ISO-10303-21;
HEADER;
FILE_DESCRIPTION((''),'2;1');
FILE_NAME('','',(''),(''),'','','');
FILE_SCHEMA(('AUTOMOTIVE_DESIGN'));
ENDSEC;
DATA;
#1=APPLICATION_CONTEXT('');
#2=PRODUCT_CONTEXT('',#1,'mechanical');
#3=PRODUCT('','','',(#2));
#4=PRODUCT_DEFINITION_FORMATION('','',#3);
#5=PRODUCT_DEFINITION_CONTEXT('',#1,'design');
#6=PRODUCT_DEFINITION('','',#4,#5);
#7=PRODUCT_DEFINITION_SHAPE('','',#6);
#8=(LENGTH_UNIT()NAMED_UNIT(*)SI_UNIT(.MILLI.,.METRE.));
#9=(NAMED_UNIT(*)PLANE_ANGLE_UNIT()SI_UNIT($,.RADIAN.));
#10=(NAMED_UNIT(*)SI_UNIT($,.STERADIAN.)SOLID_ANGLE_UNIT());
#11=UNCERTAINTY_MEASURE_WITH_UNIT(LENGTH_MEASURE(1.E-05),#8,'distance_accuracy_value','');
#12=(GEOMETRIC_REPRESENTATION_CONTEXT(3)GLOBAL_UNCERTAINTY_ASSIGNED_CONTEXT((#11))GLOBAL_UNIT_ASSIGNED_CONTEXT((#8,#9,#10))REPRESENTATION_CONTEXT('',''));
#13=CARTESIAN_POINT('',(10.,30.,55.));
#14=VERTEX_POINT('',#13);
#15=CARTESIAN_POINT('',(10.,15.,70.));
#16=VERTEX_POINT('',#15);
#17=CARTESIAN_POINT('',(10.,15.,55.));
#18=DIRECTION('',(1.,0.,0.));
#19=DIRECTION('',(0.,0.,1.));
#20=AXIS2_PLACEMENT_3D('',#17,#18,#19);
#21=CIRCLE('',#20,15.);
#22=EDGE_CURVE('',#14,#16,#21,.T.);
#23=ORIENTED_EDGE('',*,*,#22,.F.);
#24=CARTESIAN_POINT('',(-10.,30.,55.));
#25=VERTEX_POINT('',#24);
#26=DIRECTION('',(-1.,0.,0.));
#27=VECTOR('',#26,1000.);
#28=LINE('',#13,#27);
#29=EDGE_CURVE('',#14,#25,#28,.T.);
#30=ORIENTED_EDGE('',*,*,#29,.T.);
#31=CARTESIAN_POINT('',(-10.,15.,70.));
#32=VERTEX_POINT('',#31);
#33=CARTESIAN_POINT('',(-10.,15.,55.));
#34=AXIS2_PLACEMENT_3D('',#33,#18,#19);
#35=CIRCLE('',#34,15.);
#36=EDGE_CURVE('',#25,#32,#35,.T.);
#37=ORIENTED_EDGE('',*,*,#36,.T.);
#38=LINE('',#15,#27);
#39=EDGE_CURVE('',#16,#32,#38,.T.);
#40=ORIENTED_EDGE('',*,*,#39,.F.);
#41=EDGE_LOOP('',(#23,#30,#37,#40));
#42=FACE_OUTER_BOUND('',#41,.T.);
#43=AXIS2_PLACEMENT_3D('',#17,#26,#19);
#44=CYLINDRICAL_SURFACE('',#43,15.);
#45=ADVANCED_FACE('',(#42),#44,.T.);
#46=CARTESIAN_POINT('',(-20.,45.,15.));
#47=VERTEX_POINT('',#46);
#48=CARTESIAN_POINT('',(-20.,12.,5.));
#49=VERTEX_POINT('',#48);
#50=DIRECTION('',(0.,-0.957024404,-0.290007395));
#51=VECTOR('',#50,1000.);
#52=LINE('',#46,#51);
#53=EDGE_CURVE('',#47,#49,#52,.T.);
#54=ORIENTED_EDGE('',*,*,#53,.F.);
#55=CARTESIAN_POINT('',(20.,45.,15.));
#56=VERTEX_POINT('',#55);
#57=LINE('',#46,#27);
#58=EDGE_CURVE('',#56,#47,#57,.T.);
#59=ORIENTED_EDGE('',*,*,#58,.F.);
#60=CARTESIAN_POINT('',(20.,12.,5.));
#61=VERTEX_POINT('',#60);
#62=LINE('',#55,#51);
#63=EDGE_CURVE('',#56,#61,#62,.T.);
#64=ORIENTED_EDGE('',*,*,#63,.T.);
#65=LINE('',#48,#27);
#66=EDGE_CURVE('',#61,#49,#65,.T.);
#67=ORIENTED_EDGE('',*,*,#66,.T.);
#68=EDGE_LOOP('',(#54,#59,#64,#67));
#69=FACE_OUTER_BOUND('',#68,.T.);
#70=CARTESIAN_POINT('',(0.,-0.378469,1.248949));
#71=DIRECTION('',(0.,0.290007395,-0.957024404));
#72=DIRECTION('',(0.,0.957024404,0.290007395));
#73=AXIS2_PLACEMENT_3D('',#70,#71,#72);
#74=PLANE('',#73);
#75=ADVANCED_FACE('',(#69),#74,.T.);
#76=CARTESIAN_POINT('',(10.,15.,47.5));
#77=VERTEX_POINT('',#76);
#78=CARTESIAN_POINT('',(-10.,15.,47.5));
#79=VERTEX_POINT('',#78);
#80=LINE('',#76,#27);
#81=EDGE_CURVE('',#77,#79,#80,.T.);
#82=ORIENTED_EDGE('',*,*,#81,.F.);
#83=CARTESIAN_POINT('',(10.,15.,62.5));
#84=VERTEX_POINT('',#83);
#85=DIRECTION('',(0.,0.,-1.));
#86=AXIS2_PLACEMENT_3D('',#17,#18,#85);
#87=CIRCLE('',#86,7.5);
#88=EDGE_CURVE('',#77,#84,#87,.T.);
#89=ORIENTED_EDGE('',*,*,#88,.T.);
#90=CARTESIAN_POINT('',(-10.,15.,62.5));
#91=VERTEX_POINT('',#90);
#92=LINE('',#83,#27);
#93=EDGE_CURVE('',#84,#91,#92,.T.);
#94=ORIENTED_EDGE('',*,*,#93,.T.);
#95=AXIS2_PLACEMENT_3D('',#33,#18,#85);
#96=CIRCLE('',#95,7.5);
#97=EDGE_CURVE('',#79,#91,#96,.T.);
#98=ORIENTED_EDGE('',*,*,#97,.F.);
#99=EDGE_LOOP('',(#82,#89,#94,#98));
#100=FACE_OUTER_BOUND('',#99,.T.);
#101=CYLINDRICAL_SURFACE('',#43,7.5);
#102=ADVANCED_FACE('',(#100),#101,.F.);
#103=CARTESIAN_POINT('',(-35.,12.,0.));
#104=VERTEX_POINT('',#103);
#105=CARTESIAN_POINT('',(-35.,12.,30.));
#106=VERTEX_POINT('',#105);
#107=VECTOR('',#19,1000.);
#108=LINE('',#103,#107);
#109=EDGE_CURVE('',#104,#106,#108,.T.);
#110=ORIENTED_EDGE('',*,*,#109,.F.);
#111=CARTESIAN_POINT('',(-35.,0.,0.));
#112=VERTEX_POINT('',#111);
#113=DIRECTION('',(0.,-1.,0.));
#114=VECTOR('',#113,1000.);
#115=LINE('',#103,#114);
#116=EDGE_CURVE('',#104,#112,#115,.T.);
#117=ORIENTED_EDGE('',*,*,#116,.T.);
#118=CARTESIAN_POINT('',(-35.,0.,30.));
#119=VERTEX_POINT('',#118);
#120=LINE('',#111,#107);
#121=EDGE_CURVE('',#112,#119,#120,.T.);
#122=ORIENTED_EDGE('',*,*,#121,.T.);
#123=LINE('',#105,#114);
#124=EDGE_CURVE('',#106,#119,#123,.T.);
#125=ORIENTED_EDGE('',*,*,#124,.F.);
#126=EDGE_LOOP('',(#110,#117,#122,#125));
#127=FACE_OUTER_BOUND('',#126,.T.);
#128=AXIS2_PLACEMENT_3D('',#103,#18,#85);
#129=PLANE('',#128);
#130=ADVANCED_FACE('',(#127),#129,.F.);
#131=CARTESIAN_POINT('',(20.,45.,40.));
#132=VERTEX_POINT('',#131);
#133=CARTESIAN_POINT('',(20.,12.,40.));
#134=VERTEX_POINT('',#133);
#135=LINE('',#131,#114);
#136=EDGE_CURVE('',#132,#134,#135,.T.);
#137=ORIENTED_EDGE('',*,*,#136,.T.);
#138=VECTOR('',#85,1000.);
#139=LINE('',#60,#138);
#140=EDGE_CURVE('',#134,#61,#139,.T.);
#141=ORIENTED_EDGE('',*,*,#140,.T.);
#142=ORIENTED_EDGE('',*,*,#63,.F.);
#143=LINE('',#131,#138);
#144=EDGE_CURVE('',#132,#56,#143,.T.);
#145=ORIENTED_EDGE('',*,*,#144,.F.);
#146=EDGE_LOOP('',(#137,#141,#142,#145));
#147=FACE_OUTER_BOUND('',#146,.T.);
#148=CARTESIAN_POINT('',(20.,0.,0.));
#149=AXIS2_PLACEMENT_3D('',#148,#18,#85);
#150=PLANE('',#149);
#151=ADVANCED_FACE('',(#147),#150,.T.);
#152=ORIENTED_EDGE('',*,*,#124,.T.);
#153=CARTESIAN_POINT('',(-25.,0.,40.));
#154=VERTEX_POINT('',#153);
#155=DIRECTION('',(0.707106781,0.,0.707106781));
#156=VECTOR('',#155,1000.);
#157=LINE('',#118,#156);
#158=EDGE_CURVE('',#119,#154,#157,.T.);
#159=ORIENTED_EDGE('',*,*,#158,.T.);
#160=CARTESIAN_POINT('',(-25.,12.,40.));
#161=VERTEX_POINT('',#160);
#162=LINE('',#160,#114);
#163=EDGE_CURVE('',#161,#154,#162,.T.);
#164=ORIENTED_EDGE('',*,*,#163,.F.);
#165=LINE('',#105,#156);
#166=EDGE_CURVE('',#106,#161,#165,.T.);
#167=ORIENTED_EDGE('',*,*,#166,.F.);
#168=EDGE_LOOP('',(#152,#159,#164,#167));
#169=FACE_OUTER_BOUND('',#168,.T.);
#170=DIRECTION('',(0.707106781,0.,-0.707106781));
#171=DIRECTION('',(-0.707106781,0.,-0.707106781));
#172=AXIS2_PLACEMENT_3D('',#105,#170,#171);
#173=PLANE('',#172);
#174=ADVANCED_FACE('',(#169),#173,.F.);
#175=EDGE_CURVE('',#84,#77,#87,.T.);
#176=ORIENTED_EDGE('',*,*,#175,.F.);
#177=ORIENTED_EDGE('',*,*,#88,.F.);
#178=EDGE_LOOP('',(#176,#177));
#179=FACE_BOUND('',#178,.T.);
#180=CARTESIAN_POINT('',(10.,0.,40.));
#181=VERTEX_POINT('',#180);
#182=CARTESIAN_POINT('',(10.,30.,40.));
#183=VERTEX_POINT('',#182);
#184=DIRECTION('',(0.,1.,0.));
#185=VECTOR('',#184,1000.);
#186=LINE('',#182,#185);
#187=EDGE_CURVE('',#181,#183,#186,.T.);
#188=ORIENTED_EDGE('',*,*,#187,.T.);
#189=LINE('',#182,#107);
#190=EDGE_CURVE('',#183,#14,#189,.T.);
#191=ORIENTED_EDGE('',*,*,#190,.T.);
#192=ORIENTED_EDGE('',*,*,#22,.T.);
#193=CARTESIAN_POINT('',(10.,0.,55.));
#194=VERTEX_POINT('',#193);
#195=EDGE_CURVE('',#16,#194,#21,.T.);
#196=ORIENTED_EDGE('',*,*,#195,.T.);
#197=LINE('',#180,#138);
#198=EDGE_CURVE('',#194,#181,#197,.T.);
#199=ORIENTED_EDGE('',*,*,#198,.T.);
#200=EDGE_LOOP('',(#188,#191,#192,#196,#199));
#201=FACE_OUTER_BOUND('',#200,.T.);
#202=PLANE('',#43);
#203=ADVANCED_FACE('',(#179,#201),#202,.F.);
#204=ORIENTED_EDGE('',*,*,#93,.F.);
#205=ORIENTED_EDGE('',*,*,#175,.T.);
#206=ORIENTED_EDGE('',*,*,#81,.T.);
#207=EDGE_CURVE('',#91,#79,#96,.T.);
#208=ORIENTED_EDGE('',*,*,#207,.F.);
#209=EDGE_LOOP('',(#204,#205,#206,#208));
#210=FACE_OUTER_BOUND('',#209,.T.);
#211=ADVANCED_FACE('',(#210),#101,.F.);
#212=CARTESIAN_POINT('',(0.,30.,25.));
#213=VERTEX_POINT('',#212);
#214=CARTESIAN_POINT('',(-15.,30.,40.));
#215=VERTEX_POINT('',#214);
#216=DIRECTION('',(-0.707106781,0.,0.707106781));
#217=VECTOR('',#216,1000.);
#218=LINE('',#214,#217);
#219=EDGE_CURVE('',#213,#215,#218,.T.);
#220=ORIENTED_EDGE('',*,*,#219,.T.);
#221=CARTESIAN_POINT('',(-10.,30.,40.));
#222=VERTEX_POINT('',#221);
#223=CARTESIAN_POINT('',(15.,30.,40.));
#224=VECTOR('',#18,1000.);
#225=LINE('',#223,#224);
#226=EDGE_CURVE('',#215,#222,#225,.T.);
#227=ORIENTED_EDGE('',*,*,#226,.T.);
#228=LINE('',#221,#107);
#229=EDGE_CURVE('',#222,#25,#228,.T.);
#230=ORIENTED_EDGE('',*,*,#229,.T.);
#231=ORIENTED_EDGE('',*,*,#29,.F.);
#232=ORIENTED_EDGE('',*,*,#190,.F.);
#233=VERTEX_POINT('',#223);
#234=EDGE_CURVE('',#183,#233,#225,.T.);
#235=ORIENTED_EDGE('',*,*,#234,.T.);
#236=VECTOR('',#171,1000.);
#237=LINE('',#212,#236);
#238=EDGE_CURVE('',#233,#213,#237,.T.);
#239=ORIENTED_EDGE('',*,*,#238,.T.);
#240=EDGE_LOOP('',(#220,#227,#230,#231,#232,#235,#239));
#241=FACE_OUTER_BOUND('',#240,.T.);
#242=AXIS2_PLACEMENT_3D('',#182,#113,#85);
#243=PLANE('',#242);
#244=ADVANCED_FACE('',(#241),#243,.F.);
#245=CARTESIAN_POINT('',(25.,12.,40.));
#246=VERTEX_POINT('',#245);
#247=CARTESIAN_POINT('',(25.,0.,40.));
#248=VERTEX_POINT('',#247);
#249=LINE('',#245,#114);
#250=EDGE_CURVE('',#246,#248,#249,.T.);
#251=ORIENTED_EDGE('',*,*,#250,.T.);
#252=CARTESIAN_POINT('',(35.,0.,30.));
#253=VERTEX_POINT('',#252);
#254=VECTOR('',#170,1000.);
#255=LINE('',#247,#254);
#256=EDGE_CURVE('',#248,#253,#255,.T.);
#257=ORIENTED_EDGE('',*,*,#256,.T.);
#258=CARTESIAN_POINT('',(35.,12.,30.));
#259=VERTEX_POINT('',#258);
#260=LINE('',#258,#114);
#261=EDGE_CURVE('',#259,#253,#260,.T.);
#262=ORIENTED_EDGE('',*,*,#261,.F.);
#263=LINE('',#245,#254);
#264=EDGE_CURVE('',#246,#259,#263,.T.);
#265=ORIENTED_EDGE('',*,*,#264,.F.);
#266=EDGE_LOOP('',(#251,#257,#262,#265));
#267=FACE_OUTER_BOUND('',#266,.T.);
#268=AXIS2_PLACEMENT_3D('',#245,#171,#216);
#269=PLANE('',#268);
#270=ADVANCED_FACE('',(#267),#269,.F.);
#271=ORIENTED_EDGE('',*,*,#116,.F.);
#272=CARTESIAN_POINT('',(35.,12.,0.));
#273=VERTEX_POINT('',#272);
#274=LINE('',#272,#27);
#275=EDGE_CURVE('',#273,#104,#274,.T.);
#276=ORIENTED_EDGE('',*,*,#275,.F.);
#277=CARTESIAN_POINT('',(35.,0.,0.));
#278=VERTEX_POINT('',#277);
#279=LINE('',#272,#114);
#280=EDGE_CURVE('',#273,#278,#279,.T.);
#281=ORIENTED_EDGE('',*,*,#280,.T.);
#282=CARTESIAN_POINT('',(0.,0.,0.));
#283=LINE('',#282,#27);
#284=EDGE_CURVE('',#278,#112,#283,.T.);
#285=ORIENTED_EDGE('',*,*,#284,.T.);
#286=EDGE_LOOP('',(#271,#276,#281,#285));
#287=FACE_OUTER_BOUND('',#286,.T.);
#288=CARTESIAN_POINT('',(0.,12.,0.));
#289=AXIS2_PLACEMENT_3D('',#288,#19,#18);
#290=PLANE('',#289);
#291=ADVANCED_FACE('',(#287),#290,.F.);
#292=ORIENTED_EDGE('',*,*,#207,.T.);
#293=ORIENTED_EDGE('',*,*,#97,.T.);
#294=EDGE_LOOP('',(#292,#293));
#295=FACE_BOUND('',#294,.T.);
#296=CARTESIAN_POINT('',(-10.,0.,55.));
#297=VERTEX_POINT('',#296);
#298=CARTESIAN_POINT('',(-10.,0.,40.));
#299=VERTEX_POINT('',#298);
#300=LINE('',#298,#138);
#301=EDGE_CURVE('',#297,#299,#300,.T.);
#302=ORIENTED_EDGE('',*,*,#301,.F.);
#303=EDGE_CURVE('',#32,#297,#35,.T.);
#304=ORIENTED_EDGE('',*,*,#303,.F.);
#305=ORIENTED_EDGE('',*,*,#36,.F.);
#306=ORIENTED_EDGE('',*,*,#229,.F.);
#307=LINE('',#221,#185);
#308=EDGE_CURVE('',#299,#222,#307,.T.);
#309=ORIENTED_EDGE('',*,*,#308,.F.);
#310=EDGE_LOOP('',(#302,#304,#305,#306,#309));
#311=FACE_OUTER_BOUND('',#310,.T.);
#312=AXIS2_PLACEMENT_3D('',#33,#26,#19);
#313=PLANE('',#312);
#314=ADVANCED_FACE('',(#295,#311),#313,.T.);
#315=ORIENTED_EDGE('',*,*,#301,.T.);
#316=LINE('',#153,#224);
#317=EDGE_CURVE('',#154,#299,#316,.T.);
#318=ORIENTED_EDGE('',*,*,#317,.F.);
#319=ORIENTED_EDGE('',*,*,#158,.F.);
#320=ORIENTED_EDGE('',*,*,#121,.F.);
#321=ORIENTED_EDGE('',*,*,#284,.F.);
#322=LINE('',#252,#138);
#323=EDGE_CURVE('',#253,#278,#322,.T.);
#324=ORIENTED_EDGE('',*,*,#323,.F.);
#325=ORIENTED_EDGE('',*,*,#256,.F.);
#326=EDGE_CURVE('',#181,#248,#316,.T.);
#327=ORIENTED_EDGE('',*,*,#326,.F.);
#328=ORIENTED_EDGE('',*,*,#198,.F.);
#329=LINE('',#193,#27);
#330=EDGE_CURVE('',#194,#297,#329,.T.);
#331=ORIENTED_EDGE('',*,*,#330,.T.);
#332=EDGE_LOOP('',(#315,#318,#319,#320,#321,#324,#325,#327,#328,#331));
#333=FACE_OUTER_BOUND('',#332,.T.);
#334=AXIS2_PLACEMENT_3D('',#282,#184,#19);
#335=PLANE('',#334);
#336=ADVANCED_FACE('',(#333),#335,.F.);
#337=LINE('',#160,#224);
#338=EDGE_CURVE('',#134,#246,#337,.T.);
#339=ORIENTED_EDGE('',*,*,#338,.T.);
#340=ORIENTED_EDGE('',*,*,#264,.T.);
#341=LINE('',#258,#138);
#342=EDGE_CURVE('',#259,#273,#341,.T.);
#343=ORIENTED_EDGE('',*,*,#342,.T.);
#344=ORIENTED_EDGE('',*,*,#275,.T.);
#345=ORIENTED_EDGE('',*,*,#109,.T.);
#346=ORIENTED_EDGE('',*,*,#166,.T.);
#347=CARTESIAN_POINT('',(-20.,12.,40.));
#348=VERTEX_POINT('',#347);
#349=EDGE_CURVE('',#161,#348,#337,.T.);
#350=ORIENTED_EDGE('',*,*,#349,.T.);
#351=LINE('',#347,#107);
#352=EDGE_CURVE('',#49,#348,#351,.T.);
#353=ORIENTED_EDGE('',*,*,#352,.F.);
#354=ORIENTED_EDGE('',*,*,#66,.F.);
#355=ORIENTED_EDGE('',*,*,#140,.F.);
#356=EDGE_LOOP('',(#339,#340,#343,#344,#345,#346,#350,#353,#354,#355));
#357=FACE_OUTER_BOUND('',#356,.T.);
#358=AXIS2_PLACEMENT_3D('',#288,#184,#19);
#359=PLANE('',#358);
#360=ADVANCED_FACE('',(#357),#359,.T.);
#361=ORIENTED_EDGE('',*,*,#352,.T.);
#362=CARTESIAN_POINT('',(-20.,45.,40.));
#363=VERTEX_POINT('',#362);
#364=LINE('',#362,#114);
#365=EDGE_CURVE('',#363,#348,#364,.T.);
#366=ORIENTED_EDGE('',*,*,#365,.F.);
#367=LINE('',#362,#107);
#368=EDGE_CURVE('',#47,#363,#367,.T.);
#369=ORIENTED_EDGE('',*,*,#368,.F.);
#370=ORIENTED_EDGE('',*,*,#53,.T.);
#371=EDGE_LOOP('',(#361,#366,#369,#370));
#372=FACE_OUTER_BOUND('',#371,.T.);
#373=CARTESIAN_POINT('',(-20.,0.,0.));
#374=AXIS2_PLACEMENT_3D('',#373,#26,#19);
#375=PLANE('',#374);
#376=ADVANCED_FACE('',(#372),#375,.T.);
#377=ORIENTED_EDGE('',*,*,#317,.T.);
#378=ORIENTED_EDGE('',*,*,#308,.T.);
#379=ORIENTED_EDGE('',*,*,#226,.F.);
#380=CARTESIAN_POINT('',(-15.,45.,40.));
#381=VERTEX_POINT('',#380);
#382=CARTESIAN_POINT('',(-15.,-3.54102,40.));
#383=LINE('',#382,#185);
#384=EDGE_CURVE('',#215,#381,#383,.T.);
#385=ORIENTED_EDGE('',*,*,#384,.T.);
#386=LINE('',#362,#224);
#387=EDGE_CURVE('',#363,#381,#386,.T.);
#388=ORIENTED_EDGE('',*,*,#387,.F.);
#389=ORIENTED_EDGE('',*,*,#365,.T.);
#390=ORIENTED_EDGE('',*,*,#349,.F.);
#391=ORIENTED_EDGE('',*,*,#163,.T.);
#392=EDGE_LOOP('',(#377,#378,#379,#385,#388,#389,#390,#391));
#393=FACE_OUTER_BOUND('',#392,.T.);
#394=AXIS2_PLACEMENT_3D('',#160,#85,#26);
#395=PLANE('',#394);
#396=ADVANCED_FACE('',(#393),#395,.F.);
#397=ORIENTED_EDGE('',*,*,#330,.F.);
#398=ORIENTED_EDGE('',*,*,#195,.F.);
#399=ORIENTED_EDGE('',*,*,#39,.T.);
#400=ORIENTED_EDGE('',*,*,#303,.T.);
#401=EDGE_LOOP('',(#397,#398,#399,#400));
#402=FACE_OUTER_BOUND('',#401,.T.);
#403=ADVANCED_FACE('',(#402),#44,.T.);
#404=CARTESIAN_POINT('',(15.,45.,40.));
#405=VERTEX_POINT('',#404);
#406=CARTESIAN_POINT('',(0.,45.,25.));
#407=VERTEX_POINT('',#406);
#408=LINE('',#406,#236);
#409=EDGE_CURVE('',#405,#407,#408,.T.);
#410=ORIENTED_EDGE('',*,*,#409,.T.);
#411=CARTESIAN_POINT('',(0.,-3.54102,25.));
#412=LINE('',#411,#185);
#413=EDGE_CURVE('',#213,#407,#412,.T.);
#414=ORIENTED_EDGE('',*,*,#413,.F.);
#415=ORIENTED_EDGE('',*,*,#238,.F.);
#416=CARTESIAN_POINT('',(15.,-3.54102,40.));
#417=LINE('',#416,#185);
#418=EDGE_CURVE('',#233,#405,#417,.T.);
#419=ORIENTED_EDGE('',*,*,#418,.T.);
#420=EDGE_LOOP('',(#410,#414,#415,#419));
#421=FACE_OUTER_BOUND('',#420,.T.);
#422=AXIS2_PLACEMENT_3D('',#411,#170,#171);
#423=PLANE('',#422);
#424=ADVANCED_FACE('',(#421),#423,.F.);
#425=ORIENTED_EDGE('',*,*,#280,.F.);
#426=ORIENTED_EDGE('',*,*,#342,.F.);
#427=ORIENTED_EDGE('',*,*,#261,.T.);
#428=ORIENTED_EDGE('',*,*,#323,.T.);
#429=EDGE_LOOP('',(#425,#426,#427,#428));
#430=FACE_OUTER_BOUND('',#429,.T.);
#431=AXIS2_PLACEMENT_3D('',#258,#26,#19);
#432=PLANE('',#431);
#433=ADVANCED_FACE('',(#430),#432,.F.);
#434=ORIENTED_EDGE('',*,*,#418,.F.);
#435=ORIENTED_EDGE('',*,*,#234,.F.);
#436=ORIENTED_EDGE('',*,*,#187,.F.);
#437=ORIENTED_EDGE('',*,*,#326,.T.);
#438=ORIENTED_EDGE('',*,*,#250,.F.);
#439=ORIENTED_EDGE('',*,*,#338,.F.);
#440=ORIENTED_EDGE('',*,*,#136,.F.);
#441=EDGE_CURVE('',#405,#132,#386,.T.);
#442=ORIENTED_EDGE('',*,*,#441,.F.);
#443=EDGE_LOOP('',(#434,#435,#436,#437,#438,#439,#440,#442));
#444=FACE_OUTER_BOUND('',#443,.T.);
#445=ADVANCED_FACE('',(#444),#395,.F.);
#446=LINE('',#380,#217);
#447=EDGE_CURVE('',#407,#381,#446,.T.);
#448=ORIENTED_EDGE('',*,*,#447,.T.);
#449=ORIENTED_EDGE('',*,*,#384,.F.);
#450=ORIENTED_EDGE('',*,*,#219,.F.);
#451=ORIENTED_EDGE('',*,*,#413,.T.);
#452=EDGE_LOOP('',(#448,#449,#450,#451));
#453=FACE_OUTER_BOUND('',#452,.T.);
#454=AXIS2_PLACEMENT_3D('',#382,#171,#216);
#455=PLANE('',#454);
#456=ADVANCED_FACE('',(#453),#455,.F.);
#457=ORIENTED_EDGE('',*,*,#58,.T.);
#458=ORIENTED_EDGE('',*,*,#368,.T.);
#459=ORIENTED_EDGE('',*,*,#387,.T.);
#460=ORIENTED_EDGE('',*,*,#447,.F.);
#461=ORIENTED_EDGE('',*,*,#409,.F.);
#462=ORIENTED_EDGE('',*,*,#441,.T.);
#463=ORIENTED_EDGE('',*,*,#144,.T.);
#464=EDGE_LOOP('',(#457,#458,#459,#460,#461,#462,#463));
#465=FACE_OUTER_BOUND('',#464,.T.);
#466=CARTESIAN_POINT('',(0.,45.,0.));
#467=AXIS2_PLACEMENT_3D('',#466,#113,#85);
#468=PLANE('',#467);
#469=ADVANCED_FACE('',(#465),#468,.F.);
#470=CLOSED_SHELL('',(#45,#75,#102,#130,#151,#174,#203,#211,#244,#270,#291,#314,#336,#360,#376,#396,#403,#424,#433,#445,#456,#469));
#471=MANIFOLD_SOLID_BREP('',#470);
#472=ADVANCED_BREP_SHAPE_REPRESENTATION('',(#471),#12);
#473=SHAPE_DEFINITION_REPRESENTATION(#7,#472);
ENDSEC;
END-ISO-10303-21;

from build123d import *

# Parameters (mm, degrees)
BASE_PLATE_DEPTH        = 12
JOURNAL_BOSS_SKETCH_R   = 7.5
JOURNAL_BOSS_DEPTH      = 10
CRADLE_SLOT_30X15_DEPTH = 15


with BuildPart() as part:
    # Base Plate Sketch → Base Plate (new body)
    with BuildSketch(Plane(origin=(0, 0, 0), x_dir=(1, 0, 0), z_dir=(0, 1, 0))):
        Polygon((0, 0), (-35, 0), (-35, -30), (-25, -40), (25, -40), (35, -30), (35, 0), align=None)
    extrude(amount=BASE_PLATE_DEPTH)

    # Pedestal Top Profile → Tapered Pedestal section 0
    with BuildSketch(Plane(origin=(0, 45, 0), x_dir=(1, 0, 0), z_dir=(0, 1, 0))):
        with BuildLine():
            Line((-20, -40), (20, -40))
            Line((20, -40), (20, -15))
            Line((20, -15), (-20, -15))
            Line((-20, -15), (-20, -40))
        make_face()
    # Pedestal Bottom Profile → Tapered Pedestal section 1
    with BuildSketch(Plane(origin=(0, 12, 0), x_dir=(1, 0, 0), z_dir=(0, 1, 0))):
        with BuildLine():
            Line((-20, -40), (-20, -5))
            Line((-20, -5), (20, -5))
            Line((20, -5), (20, -40))
            Line((20, -40), (-20, -40))
        make_face()
    loft()

    # Journal Boss Sketch → Journal Boss (add, symmetric)
    with BuildSketch(Plane(origin=(0, 0, 0), x_dir=(0, 0, -1), z_dir=(1, 0, 0))):
        with BuildLine():
            Line((-40, 30), (-55, 30))
            ThreePointArc((-55, 30), (-70, 15), (-55, 0))
            Line((-55, 0), (-40, 0))
            Line((-40, 0), (-40, 30))
        make_face()
        with Locations((-55, 15)):
            Circle(JOURNAL_BOSS_SKETCH_R, mode=Mode.SUBTRACT)
    extrude(amount=JOURNAL_BOSS_DEPTH, both=True)

    # Cradle Slot Sketch → Cradle Slot 30x15 (cut)
    with BuildSketch(Plane(origin=(0, 45, 0), x_dir=(1, 0, 0), z_dir=(0, 1, 0))):
        Polygon((-15, -40), (0, -25), (15, -40), align=None)
    extrude(amount=-CRADLE_SLOT_30X15_DEPTH, mode=Mode.SUBTRACT)


solid = part.part
